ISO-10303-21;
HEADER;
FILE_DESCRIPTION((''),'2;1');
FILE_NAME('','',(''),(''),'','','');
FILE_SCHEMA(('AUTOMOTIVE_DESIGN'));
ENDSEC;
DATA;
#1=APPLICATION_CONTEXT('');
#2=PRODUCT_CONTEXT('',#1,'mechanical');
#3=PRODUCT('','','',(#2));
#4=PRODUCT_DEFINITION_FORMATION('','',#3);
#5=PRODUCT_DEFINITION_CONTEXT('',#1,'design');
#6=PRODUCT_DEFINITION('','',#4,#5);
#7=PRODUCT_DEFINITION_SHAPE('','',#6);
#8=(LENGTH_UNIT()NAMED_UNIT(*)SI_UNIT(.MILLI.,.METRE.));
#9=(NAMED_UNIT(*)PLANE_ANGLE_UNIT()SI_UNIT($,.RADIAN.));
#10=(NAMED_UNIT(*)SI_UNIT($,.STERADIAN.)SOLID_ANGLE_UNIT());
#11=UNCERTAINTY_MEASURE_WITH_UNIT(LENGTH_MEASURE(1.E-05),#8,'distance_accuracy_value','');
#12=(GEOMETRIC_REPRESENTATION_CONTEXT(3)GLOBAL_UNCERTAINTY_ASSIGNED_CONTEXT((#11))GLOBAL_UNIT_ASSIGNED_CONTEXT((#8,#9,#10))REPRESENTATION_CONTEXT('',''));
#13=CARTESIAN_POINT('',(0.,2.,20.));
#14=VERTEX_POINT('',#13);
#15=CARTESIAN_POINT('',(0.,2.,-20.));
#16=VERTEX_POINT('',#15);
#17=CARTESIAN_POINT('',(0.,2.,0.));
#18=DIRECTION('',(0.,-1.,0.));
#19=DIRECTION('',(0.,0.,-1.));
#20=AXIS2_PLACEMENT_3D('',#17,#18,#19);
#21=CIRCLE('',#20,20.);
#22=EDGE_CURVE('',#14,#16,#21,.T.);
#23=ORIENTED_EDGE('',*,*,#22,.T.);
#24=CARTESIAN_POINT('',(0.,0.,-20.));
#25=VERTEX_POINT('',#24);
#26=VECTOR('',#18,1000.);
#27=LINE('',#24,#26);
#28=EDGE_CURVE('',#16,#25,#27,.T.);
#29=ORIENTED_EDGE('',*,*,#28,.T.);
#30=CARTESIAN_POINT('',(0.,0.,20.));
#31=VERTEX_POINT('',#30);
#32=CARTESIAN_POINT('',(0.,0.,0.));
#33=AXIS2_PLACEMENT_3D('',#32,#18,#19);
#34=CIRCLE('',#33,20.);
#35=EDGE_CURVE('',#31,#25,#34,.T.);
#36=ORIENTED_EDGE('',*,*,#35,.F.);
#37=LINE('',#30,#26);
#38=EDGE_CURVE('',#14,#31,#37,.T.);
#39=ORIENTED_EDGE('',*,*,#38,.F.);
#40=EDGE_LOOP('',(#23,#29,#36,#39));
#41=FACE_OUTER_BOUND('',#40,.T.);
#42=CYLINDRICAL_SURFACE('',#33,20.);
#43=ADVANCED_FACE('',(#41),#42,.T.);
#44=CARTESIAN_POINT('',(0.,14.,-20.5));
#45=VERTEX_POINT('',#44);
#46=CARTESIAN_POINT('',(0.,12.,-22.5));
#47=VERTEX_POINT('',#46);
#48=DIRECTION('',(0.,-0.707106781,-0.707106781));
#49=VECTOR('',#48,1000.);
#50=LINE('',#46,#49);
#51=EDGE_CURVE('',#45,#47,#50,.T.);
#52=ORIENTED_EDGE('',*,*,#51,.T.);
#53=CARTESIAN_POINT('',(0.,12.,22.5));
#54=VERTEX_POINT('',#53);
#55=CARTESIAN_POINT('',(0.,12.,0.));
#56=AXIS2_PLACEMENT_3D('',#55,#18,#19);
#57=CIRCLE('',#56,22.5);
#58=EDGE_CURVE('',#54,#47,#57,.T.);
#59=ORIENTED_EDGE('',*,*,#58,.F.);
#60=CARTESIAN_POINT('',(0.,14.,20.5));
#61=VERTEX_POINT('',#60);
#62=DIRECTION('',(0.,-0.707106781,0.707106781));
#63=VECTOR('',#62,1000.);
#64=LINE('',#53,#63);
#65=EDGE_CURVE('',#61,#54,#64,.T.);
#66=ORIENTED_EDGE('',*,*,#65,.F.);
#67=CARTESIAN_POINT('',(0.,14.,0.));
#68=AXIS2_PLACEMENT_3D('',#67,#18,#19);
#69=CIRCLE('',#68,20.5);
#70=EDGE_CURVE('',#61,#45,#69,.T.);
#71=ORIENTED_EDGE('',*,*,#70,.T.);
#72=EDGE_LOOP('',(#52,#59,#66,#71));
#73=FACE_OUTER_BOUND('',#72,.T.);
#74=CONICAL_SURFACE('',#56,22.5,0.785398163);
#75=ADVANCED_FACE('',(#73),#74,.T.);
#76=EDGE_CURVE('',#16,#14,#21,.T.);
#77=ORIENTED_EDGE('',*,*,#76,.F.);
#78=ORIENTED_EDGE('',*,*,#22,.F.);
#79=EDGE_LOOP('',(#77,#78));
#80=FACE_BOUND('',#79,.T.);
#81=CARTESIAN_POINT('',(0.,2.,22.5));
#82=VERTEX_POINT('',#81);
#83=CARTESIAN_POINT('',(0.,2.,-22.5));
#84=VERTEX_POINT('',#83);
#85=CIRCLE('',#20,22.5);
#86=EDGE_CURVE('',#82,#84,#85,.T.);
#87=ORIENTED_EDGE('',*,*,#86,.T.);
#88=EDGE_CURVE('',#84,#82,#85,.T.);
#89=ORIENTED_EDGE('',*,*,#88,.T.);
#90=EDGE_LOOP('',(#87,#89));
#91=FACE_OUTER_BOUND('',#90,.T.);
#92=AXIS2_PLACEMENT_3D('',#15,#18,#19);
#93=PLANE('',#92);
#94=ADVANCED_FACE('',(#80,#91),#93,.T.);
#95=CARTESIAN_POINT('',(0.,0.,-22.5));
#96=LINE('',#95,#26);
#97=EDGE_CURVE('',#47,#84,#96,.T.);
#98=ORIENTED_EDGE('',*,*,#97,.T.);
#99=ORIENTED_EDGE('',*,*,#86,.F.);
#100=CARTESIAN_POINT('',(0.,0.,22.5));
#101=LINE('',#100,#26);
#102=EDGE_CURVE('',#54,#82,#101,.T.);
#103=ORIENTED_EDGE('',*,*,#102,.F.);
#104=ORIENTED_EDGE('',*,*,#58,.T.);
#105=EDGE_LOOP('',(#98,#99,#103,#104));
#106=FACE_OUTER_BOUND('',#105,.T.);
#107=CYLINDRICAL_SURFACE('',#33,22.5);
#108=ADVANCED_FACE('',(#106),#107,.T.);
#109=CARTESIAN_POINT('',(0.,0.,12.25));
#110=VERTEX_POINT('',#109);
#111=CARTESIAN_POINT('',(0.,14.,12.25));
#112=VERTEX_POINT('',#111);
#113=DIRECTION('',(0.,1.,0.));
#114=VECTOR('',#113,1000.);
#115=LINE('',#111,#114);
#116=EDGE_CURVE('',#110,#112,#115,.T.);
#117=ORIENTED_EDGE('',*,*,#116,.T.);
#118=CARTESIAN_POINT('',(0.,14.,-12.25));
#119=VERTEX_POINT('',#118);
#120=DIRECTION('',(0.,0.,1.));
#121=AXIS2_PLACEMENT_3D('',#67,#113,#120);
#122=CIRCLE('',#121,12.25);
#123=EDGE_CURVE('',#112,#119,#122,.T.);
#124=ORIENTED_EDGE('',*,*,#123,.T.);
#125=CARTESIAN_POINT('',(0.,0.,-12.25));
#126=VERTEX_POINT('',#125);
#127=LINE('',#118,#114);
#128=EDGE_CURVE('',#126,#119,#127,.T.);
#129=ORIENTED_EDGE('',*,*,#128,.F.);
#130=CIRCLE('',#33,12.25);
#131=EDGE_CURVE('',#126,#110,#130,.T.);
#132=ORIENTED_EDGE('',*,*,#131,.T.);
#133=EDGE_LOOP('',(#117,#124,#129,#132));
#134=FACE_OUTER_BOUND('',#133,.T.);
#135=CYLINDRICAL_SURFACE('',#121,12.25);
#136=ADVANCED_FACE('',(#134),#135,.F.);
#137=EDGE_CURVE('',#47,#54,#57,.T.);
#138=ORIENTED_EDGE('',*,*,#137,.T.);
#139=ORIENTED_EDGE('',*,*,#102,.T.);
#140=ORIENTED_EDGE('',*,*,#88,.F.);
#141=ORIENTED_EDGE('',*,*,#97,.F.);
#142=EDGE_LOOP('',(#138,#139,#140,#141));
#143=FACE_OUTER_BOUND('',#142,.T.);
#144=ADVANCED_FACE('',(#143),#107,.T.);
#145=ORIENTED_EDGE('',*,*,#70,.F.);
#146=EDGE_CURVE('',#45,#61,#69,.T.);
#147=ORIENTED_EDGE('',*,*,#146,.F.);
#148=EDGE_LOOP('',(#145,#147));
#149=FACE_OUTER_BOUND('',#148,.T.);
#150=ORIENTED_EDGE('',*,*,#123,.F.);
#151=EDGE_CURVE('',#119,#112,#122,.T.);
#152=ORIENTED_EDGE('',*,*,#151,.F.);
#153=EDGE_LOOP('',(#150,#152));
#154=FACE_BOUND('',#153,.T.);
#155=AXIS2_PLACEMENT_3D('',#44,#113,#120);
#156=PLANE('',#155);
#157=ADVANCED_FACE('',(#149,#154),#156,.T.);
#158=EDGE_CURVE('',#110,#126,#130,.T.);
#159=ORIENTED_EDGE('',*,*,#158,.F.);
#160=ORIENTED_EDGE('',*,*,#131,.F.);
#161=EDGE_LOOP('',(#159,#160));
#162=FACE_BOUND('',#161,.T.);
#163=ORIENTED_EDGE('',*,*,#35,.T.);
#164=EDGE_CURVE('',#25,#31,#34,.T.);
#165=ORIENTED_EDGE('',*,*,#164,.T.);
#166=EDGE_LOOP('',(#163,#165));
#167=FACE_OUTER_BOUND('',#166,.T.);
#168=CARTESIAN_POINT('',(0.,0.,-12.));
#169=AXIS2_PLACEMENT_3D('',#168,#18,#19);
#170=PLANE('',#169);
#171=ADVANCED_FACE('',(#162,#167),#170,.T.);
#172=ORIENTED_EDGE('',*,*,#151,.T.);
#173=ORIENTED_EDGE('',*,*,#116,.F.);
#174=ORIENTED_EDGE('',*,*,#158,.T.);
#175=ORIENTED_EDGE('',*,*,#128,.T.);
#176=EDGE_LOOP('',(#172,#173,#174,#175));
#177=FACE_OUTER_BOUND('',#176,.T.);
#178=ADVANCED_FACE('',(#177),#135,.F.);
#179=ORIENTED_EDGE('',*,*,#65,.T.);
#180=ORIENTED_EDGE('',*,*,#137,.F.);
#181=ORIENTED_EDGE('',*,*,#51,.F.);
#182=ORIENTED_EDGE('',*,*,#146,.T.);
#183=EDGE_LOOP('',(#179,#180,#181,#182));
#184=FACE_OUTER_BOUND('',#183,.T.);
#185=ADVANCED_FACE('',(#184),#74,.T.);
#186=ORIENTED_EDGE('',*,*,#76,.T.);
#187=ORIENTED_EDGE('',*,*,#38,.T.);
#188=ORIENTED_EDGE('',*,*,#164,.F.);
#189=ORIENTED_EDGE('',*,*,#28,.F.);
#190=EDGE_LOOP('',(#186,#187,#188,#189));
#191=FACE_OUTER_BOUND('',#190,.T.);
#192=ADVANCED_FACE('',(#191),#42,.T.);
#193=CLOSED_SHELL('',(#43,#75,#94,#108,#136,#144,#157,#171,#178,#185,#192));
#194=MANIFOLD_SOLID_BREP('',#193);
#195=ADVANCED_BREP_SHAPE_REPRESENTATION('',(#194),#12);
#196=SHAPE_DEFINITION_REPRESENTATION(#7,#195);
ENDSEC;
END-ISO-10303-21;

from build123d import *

# Parameters (mm, degrees)
G3_4_TAPPED_HOLE1_D     = 24.5
G3_4_TAPPED_HOLE1_DEPTH = 58.32
G3_4_TAPPED_HOLE1_TIP   = 7.360542583


with BuildPart() as part:
    # Sketch1 → Revolve1 (revolve)
    with BuildSketch(Plane(origin=(0, 0, 0), x_dir=(0, 0, -1), z_dir=(1, 0, 0))):
        Polygon((20, 0), (20, 2), (22.5, 2), (22.5, 12), (20.5, 14), (12, 14), (12, 0), align=None)
    revolve(axis=Axis((0, 0, 0), (0, 1, 0)))

    # G3/4 Tapped Hole1
    with Locations(Plane(origin=(0, 14, 0), x_dir=(1, 0, 0), z_dir=(0, 1, 0))):
        with Locations((0, 0)):
            Hole(G3_4_TAPPED_HOLE1_D / 2, depth=G3_4_TAPPED_HOLE1_DEPTH)
            with Locations((0, 0, -(G3_4_TAPPED_HOLE1_DEPTH + G3_4_TAPPED_HOLE1_TIP / 2))):  # 118° drill point
                Cone(0, G3_4_TAPPED_HOLE1_D / 2, G3_4_TAPPED_HOLE1_TIP, mode=Mode.SUBTRACT)


solid = part.part
